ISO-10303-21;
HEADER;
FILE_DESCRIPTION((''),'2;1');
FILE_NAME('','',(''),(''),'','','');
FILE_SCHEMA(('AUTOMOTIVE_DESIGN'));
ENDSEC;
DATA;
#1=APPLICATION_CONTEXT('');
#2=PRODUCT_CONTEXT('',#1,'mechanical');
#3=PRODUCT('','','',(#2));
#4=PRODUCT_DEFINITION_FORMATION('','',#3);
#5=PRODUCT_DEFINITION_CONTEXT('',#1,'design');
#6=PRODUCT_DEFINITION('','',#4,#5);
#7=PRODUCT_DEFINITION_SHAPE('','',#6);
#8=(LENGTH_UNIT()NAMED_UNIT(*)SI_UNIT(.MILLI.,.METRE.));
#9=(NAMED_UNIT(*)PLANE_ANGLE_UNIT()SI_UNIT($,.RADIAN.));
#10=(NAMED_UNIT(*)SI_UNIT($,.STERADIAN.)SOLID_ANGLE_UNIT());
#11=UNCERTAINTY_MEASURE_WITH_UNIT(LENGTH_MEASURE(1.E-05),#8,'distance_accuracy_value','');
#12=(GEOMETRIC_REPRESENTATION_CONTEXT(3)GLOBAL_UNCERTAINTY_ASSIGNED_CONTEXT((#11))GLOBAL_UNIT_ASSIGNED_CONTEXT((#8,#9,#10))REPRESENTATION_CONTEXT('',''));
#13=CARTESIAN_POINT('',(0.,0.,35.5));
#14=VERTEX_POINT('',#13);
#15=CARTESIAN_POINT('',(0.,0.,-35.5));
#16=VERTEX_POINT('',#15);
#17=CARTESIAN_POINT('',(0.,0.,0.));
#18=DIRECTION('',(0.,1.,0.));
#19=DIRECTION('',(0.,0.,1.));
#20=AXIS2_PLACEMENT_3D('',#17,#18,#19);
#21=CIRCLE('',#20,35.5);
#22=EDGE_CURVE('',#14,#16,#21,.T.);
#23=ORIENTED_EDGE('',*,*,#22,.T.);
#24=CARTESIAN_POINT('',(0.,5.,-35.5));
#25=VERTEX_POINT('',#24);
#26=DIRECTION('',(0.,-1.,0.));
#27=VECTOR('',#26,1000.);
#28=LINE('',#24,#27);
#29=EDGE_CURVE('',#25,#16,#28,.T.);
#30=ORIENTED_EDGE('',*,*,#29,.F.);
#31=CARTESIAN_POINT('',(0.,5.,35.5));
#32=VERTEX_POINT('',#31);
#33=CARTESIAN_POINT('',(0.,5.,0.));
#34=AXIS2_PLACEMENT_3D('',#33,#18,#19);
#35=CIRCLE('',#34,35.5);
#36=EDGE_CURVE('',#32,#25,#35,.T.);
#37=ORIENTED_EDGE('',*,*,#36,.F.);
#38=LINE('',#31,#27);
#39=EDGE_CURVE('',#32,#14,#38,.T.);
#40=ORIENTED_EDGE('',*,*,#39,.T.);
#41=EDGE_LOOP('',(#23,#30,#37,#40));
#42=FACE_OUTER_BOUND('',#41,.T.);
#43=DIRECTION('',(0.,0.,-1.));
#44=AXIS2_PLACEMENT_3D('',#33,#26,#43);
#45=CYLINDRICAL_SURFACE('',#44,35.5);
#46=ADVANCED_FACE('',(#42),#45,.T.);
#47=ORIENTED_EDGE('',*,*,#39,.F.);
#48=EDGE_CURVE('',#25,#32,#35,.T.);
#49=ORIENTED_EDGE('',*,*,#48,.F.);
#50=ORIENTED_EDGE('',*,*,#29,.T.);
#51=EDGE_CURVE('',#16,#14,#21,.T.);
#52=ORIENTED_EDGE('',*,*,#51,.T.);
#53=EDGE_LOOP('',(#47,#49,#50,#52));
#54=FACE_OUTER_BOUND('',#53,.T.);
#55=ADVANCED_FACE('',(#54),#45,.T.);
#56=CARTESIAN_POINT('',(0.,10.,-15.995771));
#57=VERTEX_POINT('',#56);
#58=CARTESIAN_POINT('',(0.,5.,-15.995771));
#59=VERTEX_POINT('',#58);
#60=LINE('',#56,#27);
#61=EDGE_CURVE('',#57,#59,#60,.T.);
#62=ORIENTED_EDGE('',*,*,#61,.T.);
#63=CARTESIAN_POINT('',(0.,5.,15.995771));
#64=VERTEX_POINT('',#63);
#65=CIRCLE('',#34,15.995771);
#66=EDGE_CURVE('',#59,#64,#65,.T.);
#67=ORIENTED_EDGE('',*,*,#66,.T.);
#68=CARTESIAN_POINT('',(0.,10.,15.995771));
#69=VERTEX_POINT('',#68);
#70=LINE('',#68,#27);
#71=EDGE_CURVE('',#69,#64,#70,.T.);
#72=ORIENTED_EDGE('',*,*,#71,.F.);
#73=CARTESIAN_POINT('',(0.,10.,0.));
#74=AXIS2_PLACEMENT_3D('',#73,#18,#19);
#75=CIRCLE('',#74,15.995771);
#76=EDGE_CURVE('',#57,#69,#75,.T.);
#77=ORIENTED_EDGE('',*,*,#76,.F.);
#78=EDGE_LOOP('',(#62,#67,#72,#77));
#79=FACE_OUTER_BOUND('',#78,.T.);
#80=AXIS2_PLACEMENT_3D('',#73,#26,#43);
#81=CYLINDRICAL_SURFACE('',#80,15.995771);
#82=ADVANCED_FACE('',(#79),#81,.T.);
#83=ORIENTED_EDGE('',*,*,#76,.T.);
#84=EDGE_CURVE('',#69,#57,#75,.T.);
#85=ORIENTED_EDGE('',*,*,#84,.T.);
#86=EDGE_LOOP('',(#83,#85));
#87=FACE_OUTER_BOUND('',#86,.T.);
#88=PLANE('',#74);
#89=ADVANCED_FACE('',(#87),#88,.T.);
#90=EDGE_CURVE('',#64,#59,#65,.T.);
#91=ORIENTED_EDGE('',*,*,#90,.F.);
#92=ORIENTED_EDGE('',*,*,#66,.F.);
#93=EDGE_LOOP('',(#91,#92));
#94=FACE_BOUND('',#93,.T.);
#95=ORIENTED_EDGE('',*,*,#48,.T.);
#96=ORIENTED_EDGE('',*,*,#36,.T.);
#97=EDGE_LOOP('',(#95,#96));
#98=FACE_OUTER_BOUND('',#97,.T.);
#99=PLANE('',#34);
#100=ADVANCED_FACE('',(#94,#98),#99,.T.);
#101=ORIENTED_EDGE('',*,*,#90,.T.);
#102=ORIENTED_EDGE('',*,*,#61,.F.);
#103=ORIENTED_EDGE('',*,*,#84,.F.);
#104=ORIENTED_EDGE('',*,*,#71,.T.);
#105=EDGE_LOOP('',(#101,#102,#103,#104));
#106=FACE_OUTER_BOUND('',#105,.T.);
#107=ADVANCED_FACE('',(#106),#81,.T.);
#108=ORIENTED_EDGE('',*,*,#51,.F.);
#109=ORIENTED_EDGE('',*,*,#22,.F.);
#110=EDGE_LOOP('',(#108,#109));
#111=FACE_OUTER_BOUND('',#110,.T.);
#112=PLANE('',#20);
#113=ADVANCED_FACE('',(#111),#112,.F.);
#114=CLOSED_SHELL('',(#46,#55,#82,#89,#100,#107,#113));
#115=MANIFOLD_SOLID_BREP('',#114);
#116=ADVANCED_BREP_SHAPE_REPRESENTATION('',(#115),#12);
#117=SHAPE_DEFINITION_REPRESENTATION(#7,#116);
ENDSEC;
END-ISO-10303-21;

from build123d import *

# Parameters (mm, degrees)
SKETCH1_R           = 35.5
BOSS_EXTRUDE1_DEPTH = 5
SKETCH2_R           = 15.995770756
BOSS_EXTRUDE2_DEPTH = 5


with BuildPart() as part:
    # Sketch1 → Boss-Extrude1 (new body)
    with BuildSketch(Plane(origin=(0, 0, 0), x_dir=(1, 0, 0), z_dir=(0, 1, 0))):
        with Locations(Location((0, 0, 0), (0, 0, 270))):
            Circle(SKETCH1_R)
    extrude(amount=BOSS_EXTRUDE1_DEPTH)

    # Sketch2 → Boss-Extrude2 (add)
    with BuildSketch(Plane(origin=(0, 5, 0), x_dir=(1, 0, 0), z_dir=(0, 1, 0))):
        with Locations(Location((0, 0, 0), (0, 0, 270))):
            Circle(SKETCH2_R)
    extrude(amount=BOSS_EXTRUDE2_DEPTH)


solid = part.part
